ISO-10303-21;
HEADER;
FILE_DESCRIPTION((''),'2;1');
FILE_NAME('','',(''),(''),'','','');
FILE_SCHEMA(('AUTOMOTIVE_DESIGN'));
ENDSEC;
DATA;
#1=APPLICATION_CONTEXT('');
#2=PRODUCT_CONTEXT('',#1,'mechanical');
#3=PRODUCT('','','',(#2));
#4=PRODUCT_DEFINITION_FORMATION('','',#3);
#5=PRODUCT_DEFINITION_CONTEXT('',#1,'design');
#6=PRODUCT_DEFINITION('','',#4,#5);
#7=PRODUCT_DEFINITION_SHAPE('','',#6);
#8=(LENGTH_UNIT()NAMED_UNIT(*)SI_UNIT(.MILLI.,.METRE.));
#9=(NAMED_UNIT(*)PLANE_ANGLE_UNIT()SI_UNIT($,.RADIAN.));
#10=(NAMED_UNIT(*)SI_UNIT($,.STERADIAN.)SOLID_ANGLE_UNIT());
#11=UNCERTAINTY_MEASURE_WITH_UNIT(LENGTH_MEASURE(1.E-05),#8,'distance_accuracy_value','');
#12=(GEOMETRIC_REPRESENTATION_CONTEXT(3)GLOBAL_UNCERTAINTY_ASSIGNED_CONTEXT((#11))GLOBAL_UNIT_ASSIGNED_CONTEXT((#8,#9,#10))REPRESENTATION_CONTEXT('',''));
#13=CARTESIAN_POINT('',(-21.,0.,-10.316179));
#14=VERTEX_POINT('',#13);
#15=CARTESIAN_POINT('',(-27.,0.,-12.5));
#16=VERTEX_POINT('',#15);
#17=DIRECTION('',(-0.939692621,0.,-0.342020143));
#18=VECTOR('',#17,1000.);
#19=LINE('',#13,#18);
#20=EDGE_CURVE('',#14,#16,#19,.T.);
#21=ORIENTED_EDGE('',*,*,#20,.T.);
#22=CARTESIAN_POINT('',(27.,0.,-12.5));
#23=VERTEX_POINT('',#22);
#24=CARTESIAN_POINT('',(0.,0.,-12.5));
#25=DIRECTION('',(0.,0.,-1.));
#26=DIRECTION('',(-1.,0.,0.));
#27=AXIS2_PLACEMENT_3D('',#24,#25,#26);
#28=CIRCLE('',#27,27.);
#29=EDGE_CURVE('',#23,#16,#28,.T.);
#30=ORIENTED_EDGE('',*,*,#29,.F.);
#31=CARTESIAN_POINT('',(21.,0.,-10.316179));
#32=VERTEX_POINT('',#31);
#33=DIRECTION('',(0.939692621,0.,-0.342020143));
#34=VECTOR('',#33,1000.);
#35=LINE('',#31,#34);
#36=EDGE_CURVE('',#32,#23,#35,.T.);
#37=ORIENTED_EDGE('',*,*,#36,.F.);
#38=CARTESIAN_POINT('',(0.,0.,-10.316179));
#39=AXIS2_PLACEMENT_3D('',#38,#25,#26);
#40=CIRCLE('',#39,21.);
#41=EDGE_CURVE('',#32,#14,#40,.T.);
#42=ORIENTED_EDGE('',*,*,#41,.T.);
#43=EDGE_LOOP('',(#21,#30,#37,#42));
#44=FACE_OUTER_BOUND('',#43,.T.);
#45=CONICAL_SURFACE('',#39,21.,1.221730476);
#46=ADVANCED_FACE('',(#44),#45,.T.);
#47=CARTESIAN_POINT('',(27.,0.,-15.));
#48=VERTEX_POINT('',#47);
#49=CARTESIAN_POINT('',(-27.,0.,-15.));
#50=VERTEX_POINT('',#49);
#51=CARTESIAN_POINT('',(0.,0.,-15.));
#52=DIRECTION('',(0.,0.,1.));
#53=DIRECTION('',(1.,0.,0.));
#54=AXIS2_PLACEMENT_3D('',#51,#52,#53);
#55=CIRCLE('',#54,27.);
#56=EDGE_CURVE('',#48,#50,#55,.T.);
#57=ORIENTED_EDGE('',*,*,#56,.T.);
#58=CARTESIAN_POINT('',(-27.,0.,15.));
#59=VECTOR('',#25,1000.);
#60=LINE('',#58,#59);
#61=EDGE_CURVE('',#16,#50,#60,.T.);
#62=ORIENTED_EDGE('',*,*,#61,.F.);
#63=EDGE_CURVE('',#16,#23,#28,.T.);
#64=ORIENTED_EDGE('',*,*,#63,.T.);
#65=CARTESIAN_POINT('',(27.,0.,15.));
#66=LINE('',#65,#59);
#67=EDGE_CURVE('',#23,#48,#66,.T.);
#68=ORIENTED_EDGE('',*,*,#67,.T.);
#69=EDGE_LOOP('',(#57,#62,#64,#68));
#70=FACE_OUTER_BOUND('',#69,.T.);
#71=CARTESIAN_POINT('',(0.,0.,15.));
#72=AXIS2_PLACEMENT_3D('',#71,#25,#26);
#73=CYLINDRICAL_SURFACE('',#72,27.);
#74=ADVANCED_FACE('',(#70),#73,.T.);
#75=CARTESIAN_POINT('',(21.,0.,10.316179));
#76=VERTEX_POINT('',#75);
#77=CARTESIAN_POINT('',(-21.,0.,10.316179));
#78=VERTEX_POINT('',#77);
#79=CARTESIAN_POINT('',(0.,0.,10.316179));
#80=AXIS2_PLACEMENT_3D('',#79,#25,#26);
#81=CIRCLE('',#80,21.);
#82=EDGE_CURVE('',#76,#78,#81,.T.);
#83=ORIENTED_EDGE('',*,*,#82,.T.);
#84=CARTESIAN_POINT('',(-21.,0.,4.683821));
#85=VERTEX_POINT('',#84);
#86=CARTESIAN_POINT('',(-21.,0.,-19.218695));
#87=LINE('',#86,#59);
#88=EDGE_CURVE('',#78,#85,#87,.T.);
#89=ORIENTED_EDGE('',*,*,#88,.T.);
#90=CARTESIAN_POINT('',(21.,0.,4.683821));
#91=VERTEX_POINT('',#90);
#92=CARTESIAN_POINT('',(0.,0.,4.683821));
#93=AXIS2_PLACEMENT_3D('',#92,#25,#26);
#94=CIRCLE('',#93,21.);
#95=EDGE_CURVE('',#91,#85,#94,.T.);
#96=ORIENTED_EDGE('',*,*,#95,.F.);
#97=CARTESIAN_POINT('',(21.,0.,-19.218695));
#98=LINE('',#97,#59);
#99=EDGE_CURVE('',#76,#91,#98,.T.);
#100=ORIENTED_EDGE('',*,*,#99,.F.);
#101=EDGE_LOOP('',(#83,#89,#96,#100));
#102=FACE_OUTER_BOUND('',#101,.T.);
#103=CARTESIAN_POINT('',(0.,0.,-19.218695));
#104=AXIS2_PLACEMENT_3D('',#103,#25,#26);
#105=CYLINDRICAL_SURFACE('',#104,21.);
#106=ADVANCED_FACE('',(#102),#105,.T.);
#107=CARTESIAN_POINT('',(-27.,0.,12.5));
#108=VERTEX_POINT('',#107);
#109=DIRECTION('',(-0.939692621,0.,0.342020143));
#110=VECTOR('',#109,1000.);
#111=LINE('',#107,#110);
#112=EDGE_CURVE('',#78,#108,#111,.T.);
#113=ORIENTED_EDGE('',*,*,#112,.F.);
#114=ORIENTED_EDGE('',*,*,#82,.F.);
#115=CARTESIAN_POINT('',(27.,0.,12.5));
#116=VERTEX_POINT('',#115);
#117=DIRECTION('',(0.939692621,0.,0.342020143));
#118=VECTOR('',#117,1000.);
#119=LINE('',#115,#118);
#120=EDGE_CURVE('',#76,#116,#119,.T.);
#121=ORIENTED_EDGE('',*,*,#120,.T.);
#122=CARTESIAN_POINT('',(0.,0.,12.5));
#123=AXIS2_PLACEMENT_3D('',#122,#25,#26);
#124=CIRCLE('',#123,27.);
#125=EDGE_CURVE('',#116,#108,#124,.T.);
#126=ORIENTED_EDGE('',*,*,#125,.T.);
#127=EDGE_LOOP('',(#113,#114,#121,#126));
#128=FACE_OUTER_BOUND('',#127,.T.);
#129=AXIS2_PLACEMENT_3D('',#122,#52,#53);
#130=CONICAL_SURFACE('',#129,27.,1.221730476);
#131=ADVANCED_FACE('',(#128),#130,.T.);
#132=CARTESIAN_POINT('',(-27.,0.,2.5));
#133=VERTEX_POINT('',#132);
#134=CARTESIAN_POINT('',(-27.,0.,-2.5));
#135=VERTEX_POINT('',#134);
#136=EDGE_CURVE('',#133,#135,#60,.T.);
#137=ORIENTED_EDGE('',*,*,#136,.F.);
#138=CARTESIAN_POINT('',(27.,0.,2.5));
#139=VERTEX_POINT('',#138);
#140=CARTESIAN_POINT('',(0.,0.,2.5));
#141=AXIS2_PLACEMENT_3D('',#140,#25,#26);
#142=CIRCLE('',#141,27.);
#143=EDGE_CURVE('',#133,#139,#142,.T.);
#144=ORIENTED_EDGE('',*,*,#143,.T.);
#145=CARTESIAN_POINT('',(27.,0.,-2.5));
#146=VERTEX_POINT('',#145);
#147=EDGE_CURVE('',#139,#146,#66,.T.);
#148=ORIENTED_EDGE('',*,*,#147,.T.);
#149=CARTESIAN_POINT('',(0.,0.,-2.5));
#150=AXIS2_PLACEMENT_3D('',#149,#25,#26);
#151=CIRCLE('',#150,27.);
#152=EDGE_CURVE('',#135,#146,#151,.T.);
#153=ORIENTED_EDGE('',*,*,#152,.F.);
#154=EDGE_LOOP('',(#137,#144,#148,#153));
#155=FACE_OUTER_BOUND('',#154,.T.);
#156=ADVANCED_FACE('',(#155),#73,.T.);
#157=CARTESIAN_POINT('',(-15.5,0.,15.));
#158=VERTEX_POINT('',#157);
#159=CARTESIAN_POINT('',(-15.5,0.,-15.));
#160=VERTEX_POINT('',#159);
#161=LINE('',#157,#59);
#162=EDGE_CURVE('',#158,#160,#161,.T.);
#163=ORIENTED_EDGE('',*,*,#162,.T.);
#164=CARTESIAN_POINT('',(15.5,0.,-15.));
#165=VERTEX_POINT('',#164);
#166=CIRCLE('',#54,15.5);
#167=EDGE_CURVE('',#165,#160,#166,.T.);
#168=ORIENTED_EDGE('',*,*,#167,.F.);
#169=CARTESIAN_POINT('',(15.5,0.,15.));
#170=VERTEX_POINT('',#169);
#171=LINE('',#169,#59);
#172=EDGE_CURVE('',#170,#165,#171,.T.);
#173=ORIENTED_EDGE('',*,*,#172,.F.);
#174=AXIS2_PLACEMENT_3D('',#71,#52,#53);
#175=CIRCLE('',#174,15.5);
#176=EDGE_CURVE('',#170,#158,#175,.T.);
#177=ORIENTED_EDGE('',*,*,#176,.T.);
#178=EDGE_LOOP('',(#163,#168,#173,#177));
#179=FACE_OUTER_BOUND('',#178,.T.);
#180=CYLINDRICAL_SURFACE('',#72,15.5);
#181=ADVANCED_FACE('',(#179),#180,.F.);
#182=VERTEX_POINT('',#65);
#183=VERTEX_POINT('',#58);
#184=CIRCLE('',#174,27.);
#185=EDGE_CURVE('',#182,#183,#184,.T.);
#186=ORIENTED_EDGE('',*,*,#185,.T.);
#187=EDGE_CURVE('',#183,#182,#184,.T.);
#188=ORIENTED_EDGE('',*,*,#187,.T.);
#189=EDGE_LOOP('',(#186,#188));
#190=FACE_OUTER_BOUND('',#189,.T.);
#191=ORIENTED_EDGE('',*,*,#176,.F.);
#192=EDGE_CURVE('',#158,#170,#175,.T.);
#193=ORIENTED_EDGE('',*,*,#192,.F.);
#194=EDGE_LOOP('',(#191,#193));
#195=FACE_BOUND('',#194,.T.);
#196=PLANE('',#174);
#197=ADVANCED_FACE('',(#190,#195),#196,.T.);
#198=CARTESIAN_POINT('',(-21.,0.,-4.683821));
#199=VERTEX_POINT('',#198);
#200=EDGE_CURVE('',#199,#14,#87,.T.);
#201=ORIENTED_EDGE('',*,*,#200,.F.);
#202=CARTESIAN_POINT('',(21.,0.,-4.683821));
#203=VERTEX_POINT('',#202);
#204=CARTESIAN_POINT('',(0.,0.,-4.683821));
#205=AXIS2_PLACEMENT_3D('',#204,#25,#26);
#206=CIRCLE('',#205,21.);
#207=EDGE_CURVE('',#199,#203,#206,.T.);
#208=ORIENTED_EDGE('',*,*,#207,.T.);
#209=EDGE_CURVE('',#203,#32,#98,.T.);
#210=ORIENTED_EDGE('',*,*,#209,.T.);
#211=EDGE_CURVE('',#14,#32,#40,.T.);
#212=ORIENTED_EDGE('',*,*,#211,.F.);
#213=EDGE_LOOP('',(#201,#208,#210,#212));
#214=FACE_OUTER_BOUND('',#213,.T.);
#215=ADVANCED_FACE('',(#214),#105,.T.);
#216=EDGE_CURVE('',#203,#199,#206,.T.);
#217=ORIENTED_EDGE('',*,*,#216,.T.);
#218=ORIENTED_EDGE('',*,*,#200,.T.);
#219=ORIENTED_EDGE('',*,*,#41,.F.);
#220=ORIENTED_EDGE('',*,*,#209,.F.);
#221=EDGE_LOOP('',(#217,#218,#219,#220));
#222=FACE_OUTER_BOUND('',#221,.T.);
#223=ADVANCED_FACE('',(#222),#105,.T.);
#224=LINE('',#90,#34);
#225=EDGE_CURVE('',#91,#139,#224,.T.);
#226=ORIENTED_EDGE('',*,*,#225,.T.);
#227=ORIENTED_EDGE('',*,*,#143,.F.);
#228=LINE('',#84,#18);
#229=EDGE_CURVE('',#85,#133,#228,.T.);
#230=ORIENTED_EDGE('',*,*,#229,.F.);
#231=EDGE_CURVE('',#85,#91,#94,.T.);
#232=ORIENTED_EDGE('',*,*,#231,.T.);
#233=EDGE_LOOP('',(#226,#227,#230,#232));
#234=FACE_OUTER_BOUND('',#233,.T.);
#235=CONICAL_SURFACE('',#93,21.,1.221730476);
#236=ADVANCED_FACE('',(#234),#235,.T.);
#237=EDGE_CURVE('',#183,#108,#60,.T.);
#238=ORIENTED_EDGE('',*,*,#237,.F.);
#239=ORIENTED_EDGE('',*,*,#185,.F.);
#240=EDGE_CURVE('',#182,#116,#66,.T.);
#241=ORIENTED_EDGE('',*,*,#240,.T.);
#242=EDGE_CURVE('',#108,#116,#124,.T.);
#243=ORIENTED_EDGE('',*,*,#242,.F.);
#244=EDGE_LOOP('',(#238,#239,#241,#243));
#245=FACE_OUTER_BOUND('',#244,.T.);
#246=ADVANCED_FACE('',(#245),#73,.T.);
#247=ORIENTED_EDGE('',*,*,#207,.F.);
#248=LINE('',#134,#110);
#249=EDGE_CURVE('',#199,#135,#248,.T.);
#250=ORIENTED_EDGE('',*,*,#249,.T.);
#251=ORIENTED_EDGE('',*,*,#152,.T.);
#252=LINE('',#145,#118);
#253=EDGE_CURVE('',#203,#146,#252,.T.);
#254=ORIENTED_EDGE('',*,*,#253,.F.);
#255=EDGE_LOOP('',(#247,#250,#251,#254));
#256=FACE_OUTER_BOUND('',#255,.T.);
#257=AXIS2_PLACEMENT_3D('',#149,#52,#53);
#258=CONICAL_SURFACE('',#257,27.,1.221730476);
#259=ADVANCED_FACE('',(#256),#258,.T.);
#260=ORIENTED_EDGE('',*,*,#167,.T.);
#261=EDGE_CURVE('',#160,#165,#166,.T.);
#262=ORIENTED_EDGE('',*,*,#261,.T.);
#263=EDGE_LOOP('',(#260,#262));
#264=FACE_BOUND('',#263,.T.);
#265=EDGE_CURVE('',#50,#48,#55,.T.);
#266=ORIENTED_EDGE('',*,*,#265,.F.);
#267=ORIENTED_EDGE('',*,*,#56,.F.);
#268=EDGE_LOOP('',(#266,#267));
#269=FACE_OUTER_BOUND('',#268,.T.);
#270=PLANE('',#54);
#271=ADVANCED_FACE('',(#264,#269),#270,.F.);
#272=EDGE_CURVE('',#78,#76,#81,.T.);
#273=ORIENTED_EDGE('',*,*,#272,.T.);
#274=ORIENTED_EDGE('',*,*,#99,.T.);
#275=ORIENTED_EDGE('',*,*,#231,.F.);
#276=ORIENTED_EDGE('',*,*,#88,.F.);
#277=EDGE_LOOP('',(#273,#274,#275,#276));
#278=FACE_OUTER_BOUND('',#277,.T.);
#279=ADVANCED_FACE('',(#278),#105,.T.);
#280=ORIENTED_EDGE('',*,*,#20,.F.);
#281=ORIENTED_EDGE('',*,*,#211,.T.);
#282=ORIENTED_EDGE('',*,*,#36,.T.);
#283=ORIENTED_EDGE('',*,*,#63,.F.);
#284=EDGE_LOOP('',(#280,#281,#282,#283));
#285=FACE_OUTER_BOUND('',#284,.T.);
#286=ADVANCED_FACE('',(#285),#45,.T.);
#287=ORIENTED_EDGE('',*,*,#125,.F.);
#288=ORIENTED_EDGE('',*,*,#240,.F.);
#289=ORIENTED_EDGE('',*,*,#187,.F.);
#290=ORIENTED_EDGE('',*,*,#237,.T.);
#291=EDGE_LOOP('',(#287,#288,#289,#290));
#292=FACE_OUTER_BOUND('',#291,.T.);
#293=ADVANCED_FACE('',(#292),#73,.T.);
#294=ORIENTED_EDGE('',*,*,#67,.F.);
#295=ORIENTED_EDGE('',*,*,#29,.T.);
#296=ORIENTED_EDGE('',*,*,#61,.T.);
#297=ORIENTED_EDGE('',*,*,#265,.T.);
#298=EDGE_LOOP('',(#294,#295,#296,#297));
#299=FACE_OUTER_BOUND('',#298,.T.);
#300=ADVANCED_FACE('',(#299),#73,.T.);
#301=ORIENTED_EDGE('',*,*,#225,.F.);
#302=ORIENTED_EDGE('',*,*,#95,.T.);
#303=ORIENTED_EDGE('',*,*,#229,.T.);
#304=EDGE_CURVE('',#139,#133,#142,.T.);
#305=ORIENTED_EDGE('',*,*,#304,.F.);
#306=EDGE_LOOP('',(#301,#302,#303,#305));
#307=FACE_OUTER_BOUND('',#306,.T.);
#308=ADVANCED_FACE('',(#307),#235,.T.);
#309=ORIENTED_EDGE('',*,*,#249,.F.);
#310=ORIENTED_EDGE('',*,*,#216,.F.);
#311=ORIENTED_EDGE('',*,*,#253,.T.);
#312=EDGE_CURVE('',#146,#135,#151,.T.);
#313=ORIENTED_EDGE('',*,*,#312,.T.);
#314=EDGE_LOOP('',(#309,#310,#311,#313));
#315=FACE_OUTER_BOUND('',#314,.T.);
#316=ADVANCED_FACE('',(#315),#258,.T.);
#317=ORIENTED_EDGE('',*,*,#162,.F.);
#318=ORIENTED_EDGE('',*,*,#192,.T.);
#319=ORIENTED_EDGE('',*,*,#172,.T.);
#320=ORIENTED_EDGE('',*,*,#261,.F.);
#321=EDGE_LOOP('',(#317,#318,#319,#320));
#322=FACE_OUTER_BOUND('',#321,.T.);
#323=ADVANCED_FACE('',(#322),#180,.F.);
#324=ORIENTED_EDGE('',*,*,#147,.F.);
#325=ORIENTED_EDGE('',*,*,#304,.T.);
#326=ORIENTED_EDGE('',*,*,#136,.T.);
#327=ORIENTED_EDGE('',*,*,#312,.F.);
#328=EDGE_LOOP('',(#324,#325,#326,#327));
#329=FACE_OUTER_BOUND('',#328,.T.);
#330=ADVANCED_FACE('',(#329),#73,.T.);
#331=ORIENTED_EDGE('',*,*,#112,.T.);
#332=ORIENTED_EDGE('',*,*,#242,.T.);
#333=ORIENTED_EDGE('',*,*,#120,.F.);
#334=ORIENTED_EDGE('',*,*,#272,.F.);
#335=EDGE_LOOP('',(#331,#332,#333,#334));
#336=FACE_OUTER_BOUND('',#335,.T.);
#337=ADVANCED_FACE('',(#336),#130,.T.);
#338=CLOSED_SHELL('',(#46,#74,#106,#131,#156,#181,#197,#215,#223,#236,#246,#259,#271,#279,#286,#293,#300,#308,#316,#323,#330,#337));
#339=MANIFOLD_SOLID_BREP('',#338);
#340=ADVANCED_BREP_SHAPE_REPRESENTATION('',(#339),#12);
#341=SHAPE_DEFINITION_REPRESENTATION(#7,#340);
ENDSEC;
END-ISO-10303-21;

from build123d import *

# Parameters (mm, degrees)
SKETCH1_R           = 27
SKETCH1_R_2         = 15.5
BOSS_EXTRUDE1_DEPTH = 15


with BuildPart() as part:
    # Sketch1 → Boss-Extrude1 (new, symmetric)
    with BuildSketch(Plane.XY):
        Circle(SKETCH1_R)
        Circle(SKETCH1_R_2, mode=Mode.SUBTRACT)
    extrude(amount=BOSS_EXTRUDE1_DEPTH, both=True)

    # Sketch2 → Cut-Revolve1 (revolve, cut)
    with BuildSketch(Plane(origin=(0, 0, 0), x_dir=(1, 0, 0), z_dir=(0, 1, 0))):
        Polygon((-27, -2.5), (-27, -12.5), (-21, -10.316178594), (-21, -4.683821406), align=None)
        Polygon((-27, 2.5), (-21, 4.683821406), (-21, 10.316178594), (-27, 12.5), align=None)
    revolve(axis=Axis((0, 0, -19.218694813), (0, 0, 1)), mode=Mode.SUBTRACT)


solid = part.part
